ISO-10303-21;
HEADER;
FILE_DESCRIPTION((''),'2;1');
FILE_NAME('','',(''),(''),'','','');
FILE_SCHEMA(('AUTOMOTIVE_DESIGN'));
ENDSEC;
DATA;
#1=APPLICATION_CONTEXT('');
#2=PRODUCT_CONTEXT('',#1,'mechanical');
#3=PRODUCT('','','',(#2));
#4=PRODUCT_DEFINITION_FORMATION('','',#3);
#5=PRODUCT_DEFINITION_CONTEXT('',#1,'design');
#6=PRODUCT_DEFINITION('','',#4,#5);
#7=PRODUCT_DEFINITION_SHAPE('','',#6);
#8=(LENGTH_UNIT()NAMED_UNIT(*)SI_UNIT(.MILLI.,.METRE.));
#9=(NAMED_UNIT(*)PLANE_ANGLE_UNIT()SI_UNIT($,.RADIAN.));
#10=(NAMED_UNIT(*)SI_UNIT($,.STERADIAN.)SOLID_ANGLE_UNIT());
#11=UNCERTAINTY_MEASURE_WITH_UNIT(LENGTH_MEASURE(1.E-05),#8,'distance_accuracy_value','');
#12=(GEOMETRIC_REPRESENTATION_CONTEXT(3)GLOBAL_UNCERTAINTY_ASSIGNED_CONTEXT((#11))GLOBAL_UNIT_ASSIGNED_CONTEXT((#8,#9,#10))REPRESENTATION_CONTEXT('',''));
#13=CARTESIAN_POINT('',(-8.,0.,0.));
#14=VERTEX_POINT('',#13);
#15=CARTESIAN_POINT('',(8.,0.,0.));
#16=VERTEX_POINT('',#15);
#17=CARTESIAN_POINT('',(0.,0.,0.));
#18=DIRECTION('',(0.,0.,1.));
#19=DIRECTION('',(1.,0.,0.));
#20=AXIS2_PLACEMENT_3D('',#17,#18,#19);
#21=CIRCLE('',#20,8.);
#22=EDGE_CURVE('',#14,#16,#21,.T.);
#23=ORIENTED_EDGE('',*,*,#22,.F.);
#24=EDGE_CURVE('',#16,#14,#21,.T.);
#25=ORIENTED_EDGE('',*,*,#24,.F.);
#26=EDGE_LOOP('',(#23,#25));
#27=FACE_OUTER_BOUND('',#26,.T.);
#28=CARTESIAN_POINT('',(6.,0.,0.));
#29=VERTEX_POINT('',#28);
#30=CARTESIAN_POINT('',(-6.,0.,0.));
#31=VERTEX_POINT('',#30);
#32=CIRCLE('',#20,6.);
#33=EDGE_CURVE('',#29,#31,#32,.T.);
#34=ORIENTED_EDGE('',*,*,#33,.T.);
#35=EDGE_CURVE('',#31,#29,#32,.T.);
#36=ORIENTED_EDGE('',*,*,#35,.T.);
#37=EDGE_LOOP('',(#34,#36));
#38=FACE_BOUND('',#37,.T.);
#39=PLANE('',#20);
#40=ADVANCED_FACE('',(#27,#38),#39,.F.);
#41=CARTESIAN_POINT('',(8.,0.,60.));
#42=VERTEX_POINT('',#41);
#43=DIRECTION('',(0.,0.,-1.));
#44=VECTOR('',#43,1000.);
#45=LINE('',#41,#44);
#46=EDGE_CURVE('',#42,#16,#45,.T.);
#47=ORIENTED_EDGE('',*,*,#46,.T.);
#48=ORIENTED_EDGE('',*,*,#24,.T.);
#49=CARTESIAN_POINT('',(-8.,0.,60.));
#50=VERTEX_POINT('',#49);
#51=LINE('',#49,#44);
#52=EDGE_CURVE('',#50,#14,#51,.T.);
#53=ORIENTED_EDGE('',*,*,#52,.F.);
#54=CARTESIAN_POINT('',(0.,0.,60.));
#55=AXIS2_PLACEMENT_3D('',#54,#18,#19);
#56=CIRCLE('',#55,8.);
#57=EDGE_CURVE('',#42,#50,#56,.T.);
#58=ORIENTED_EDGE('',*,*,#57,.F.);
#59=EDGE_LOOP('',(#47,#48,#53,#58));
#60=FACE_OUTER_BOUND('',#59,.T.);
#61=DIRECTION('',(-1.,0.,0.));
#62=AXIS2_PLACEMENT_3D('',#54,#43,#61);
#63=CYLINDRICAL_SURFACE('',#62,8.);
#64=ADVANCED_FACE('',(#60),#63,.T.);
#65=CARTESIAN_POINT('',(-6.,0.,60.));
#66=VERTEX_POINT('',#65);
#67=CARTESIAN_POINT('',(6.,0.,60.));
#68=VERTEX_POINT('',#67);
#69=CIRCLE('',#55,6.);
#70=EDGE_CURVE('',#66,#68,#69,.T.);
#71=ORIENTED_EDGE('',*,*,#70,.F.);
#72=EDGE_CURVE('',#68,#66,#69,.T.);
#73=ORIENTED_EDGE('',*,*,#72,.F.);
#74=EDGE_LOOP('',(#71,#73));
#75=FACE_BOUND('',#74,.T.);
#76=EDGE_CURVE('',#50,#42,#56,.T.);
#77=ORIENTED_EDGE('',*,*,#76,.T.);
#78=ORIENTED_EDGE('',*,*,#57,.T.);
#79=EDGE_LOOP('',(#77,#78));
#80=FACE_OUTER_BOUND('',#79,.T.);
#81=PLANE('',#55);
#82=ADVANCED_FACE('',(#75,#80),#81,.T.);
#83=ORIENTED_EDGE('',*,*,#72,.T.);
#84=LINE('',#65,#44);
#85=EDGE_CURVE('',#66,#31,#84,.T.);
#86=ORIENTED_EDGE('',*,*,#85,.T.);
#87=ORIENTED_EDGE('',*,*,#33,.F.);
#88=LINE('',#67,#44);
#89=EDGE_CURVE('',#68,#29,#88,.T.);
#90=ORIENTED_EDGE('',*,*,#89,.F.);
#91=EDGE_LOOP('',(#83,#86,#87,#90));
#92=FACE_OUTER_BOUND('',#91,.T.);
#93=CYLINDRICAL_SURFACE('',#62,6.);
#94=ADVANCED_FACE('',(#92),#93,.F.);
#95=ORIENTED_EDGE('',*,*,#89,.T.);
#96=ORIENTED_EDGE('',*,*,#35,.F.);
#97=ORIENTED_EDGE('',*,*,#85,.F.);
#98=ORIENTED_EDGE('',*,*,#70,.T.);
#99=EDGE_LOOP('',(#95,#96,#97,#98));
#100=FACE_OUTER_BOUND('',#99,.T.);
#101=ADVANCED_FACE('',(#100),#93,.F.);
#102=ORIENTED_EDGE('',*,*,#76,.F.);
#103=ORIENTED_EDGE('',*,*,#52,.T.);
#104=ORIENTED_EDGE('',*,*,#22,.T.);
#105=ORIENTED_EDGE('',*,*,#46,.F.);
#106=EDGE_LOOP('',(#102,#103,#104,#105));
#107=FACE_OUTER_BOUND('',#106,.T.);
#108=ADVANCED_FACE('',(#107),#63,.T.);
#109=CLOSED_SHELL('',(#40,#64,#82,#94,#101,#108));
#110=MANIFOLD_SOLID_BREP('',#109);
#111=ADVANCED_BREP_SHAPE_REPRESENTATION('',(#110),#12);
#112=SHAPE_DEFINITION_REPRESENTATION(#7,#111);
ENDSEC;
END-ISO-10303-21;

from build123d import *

# Parameters (mm, degrees)
SKETCH_1_R      = 8
SKETCH_1_R_2    = 6
EXTRUDE_1_DEPTH = 60


with BuildPart() as part:
    # 草图1 → 凸台-拉伸1 (new body)
    with BuildSketch(Plane.XY):
        Circle(SKETCH_1_R)
        Circle(SKETCH_1_R_2, mode=Mode.SUBTRACT)
    extrude(amount=EXTRUDE_1_DEPTH)


solid = part.part
